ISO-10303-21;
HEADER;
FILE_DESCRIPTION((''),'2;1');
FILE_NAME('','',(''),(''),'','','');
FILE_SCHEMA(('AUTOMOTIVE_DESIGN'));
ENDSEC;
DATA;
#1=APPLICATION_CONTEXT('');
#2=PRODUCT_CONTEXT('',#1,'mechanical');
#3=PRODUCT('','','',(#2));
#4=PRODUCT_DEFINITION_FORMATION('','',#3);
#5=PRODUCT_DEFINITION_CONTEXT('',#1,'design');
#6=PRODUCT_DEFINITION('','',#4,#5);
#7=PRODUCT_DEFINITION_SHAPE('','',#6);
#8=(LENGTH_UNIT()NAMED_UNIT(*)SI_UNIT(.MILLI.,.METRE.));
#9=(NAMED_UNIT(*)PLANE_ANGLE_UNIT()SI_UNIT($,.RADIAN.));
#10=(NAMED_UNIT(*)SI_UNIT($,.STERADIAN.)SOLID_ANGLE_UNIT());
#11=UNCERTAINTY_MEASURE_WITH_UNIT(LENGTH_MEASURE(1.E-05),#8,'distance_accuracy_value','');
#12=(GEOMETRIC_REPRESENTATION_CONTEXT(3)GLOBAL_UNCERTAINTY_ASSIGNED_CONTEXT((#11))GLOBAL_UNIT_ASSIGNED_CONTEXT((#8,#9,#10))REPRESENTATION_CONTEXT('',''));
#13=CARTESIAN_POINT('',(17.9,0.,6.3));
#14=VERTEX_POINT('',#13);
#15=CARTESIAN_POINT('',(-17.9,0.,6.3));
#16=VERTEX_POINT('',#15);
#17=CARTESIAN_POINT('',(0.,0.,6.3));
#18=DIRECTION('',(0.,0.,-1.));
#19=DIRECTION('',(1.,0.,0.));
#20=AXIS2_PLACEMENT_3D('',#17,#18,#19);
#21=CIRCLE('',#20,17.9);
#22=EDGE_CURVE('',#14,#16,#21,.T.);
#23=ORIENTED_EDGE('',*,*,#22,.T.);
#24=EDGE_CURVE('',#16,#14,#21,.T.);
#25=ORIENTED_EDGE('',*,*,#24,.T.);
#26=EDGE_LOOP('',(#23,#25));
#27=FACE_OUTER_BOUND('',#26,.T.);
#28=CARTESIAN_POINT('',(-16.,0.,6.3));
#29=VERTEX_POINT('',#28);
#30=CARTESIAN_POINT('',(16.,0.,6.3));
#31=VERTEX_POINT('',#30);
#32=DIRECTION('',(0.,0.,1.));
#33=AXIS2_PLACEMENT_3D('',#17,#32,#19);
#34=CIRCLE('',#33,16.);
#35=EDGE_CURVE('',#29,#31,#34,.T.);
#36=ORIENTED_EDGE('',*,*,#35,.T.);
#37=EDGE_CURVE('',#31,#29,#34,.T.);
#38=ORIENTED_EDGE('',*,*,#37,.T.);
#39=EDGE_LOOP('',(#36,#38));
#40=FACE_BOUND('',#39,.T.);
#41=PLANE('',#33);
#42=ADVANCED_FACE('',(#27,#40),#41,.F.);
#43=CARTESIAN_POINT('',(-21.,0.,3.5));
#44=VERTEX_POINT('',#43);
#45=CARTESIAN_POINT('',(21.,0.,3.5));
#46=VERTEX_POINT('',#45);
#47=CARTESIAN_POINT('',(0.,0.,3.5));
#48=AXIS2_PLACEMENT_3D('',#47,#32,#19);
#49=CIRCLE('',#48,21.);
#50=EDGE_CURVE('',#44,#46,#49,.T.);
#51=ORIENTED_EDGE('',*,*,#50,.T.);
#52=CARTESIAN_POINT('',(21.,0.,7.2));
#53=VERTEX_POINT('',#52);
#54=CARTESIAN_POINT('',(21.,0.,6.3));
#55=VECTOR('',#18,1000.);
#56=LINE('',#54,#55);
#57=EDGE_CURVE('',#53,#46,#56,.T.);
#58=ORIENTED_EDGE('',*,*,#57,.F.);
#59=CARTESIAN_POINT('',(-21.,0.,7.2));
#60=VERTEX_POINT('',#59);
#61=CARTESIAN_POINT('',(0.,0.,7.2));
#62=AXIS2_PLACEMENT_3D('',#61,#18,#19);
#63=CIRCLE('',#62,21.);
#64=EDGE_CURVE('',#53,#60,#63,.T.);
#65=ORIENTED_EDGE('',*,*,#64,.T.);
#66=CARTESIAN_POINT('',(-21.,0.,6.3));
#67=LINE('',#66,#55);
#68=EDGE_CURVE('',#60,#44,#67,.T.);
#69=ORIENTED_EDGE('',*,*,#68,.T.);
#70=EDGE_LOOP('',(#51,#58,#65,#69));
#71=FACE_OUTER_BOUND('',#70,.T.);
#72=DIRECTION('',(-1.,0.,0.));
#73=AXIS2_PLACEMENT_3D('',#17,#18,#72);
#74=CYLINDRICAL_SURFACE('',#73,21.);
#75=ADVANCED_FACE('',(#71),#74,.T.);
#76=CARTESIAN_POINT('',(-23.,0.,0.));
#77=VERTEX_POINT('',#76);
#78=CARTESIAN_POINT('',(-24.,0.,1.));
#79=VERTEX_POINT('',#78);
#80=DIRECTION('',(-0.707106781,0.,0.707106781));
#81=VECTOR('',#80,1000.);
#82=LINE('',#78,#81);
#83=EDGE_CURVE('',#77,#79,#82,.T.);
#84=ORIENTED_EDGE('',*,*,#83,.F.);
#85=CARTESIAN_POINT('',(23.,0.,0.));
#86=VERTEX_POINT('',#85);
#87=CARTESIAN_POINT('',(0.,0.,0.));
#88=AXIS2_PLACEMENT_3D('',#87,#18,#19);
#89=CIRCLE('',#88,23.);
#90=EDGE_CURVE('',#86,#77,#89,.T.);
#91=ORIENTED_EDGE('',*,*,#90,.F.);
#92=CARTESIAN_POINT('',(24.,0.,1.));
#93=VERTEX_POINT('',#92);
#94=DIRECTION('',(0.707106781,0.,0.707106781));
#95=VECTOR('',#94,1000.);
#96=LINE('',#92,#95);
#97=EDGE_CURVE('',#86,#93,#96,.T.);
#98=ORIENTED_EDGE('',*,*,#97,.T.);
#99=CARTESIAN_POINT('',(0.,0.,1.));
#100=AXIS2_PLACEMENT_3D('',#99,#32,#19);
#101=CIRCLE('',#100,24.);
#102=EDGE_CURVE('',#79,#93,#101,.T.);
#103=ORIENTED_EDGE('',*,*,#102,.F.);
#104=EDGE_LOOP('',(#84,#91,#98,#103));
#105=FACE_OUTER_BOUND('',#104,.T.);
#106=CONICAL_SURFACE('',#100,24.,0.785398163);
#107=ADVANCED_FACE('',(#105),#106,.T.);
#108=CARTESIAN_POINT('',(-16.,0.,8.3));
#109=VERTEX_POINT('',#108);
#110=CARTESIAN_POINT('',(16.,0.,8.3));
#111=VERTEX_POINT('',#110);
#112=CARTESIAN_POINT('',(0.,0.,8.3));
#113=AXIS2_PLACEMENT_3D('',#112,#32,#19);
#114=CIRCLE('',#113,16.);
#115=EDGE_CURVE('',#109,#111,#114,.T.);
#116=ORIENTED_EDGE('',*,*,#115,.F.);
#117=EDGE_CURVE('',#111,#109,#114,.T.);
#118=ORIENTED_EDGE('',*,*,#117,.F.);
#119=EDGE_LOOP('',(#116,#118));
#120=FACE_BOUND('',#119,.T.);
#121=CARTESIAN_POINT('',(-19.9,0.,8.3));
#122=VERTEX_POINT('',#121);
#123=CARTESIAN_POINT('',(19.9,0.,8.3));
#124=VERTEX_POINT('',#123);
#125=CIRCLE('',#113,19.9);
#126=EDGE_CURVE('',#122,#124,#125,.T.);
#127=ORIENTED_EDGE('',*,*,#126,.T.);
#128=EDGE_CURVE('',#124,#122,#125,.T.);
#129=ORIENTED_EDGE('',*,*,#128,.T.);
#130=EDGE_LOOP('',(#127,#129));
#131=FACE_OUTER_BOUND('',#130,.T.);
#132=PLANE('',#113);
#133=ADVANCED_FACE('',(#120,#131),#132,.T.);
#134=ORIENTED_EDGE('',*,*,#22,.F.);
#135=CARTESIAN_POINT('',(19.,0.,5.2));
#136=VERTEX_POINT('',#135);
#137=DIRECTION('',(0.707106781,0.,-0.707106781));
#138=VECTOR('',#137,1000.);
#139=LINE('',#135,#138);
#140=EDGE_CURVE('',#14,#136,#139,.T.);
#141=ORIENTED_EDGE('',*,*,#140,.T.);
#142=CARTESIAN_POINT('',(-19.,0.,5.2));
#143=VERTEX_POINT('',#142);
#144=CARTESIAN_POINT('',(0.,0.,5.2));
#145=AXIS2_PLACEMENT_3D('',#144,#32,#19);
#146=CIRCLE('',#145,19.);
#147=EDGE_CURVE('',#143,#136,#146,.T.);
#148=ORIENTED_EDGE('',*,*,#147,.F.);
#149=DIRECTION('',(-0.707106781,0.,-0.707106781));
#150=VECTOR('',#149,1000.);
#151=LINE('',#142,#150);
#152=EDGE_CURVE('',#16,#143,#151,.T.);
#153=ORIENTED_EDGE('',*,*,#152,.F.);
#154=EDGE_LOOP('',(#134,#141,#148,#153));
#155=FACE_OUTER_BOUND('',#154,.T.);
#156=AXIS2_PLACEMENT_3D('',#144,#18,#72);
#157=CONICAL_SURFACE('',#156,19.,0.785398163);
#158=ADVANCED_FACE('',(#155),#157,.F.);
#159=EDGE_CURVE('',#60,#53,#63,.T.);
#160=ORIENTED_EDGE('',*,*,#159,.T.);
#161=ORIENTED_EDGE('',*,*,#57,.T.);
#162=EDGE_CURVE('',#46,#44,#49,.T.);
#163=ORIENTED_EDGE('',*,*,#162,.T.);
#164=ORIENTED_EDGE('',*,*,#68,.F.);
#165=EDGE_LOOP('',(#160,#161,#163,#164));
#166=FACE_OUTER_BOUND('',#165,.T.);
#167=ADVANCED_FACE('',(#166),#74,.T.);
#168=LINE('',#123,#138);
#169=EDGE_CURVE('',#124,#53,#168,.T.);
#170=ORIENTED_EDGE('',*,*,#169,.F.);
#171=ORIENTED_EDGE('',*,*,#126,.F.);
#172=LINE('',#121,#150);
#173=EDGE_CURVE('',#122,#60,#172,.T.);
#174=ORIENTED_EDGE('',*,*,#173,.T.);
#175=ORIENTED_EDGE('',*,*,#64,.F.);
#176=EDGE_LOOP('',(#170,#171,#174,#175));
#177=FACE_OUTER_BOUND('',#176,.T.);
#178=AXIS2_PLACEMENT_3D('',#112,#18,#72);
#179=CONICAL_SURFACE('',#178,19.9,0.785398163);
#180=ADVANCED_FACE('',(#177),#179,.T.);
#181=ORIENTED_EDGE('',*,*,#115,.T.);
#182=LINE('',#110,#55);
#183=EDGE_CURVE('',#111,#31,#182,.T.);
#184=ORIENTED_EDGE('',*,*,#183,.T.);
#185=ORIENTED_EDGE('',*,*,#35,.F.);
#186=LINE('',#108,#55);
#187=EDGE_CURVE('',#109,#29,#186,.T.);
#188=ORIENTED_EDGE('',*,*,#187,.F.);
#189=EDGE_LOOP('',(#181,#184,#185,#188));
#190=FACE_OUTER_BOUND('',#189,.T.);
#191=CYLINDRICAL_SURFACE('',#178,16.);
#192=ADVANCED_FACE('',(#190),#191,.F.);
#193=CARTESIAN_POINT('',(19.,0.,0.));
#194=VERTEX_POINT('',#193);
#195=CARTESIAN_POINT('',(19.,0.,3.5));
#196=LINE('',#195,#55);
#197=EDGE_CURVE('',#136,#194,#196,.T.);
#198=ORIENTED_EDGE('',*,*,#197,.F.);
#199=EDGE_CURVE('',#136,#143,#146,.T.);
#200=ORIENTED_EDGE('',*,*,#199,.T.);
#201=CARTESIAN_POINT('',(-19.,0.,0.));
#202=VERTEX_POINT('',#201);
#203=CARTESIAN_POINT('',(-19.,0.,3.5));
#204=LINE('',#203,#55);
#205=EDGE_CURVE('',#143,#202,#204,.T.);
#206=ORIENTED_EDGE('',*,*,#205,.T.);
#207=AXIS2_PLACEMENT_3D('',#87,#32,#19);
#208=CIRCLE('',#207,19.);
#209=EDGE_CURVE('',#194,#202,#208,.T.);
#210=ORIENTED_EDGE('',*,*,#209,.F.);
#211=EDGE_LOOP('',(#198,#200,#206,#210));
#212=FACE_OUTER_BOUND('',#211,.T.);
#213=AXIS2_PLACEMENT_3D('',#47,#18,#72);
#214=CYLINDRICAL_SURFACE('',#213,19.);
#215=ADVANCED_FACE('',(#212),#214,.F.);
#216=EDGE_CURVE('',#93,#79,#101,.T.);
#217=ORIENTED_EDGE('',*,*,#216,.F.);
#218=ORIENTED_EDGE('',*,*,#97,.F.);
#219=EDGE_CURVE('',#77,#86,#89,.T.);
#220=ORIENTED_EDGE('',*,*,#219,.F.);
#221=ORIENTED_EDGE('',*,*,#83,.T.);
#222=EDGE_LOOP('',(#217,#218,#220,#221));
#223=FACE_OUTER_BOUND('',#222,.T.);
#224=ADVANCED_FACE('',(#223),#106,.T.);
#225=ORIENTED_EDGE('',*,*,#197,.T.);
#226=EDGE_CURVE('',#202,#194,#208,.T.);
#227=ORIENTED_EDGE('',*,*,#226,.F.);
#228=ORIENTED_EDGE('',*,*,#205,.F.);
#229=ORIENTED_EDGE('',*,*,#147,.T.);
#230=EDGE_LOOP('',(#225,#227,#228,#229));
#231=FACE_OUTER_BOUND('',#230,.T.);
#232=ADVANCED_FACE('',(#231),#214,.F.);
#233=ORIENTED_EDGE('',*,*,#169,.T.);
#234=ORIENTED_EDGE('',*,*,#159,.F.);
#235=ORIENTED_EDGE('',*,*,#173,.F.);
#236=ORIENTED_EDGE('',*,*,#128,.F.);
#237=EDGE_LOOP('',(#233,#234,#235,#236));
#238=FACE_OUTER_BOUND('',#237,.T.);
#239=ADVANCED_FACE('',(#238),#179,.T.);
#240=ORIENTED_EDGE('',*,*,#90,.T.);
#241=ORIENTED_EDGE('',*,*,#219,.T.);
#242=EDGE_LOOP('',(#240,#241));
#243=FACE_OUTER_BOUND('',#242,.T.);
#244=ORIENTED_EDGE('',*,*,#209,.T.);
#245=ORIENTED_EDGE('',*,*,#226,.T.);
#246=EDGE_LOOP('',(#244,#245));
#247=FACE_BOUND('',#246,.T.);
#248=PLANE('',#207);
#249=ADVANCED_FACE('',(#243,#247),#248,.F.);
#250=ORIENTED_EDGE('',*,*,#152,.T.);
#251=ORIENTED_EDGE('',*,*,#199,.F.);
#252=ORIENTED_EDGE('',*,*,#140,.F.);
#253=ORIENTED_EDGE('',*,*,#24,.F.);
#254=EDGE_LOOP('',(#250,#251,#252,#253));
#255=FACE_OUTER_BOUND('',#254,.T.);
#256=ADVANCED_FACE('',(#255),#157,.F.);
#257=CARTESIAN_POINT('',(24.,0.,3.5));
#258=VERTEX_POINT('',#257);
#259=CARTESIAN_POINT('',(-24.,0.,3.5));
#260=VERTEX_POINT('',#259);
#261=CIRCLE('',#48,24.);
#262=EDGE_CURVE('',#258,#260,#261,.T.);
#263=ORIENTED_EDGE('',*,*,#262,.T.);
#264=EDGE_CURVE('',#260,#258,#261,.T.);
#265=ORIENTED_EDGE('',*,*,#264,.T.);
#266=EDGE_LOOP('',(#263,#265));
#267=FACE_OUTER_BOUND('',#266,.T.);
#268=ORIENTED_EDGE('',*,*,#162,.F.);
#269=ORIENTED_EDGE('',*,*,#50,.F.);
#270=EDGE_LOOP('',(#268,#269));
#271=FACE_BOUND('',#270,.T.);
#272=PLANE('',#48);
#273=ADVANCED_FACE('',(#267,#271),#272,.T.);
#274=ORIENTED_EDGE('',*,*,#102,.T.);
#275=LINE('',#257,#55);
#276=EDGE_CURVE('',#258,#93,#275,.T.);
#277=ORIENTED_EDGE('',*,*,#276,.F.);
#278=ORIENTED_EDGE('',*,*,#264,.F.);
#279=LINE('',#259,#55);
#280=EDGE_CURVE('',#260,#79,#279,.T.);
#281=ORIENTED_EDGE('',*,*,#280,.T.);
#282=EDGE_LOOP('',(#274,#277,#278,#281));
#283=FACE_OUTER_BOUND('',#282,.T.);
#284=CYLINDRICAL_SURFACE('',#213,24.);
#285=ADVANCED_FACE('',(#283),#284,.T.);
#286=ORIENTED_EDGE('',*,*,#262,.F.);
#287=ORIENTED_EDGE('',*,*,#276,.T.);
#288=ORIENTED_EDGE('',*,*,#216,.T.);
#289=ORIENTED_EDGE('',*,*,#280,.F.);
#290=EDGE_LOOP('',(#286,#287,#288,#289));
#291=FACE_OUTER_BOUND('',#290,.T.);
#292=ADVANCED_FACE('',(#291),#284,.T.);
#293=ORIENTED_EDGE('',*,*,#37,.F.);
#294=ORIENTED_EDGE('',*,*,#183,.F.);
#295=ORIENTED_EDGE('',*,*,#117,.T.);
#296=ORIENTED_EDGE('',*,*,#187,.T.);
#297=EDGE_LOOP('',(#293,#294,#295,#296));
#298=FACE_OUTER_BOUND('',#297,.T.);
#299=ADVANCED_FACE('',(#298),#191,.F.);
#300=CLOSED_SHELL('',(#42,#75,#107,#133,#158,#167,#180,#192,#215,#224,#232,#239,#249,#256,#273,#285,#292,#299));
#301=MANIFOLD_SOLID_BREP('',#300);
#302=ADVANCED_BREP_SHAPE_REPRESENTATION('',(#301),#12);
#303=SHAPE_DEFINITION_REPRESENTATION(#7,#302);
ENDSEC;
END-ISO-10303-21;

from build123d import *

# Parameters (mm, degrees)
SKETCH_1_R      = 24
SKETCH_1_R_2    = 19
EXTRUDE_1_DEPTH = 3.5
SKETCH_2_R      = 21
SKETCH_2_R_2    = 19
EXTRUDE_2_DEPTH = 2.8
SKETCH_3_R      = 21
SKETCH_3_R_2    = 16
EXTRUDE_3_DEPTH = 2
CHAMFER_1_SIZE  = 1.1
CHAMFER_2_SIZE  = 1


with BuildPart() as part:
    # 草图1 → 凸台-拉伸1 (new body)
    with BuildSketch(Plane.XY):
        Circle(SKETCH_1_R)
        Circle(SKETCH_1_R_2, mode=Mode.SUBTRACT)
    extrude(amount=EXTRUDE_1_DEPTH)

    # 草图2 → 凸台-拉伸2 (add)
    with BuildSketch(Plane.XY.offset(3.5)):
        Circle(SKETCH_2_R)
        Circle(SKETCH_2_R_2, mode=Mode.SUBTRACT)
    extrude(amount=EXTRUDE_2_DEPTH)

    # 草图3 → 凸台-拉伸3 (add)
    with BuildSketch(Plane.XY.offset(6.3)):
        Circle(SKETCH_3_R)
        Circle(SKETCH_3_R_2, mode=Mode.SUBTRACT)
    extrude(amount=EXTRUDE_3_DEPTH)

    # 倒角1
    chamfer_1_edges = [part.edges().sort_by_distance(p)[0] for p in [
        (-21, 0, 8.3),
        (-19, 0, 6.3),
    ]]
    chamfer(chamfer_1_edges, length=CHAMFER_1_SIZE)

    # 倒角2
    chamfer_2_edges = [part.edges().sort_by_distance(p)[0] for p in [
        (-24, 0, 0),
    ]]
    chamfer(chamfer_2_edges, length=CHAMFER_2_SIZE)


solid = part.part
